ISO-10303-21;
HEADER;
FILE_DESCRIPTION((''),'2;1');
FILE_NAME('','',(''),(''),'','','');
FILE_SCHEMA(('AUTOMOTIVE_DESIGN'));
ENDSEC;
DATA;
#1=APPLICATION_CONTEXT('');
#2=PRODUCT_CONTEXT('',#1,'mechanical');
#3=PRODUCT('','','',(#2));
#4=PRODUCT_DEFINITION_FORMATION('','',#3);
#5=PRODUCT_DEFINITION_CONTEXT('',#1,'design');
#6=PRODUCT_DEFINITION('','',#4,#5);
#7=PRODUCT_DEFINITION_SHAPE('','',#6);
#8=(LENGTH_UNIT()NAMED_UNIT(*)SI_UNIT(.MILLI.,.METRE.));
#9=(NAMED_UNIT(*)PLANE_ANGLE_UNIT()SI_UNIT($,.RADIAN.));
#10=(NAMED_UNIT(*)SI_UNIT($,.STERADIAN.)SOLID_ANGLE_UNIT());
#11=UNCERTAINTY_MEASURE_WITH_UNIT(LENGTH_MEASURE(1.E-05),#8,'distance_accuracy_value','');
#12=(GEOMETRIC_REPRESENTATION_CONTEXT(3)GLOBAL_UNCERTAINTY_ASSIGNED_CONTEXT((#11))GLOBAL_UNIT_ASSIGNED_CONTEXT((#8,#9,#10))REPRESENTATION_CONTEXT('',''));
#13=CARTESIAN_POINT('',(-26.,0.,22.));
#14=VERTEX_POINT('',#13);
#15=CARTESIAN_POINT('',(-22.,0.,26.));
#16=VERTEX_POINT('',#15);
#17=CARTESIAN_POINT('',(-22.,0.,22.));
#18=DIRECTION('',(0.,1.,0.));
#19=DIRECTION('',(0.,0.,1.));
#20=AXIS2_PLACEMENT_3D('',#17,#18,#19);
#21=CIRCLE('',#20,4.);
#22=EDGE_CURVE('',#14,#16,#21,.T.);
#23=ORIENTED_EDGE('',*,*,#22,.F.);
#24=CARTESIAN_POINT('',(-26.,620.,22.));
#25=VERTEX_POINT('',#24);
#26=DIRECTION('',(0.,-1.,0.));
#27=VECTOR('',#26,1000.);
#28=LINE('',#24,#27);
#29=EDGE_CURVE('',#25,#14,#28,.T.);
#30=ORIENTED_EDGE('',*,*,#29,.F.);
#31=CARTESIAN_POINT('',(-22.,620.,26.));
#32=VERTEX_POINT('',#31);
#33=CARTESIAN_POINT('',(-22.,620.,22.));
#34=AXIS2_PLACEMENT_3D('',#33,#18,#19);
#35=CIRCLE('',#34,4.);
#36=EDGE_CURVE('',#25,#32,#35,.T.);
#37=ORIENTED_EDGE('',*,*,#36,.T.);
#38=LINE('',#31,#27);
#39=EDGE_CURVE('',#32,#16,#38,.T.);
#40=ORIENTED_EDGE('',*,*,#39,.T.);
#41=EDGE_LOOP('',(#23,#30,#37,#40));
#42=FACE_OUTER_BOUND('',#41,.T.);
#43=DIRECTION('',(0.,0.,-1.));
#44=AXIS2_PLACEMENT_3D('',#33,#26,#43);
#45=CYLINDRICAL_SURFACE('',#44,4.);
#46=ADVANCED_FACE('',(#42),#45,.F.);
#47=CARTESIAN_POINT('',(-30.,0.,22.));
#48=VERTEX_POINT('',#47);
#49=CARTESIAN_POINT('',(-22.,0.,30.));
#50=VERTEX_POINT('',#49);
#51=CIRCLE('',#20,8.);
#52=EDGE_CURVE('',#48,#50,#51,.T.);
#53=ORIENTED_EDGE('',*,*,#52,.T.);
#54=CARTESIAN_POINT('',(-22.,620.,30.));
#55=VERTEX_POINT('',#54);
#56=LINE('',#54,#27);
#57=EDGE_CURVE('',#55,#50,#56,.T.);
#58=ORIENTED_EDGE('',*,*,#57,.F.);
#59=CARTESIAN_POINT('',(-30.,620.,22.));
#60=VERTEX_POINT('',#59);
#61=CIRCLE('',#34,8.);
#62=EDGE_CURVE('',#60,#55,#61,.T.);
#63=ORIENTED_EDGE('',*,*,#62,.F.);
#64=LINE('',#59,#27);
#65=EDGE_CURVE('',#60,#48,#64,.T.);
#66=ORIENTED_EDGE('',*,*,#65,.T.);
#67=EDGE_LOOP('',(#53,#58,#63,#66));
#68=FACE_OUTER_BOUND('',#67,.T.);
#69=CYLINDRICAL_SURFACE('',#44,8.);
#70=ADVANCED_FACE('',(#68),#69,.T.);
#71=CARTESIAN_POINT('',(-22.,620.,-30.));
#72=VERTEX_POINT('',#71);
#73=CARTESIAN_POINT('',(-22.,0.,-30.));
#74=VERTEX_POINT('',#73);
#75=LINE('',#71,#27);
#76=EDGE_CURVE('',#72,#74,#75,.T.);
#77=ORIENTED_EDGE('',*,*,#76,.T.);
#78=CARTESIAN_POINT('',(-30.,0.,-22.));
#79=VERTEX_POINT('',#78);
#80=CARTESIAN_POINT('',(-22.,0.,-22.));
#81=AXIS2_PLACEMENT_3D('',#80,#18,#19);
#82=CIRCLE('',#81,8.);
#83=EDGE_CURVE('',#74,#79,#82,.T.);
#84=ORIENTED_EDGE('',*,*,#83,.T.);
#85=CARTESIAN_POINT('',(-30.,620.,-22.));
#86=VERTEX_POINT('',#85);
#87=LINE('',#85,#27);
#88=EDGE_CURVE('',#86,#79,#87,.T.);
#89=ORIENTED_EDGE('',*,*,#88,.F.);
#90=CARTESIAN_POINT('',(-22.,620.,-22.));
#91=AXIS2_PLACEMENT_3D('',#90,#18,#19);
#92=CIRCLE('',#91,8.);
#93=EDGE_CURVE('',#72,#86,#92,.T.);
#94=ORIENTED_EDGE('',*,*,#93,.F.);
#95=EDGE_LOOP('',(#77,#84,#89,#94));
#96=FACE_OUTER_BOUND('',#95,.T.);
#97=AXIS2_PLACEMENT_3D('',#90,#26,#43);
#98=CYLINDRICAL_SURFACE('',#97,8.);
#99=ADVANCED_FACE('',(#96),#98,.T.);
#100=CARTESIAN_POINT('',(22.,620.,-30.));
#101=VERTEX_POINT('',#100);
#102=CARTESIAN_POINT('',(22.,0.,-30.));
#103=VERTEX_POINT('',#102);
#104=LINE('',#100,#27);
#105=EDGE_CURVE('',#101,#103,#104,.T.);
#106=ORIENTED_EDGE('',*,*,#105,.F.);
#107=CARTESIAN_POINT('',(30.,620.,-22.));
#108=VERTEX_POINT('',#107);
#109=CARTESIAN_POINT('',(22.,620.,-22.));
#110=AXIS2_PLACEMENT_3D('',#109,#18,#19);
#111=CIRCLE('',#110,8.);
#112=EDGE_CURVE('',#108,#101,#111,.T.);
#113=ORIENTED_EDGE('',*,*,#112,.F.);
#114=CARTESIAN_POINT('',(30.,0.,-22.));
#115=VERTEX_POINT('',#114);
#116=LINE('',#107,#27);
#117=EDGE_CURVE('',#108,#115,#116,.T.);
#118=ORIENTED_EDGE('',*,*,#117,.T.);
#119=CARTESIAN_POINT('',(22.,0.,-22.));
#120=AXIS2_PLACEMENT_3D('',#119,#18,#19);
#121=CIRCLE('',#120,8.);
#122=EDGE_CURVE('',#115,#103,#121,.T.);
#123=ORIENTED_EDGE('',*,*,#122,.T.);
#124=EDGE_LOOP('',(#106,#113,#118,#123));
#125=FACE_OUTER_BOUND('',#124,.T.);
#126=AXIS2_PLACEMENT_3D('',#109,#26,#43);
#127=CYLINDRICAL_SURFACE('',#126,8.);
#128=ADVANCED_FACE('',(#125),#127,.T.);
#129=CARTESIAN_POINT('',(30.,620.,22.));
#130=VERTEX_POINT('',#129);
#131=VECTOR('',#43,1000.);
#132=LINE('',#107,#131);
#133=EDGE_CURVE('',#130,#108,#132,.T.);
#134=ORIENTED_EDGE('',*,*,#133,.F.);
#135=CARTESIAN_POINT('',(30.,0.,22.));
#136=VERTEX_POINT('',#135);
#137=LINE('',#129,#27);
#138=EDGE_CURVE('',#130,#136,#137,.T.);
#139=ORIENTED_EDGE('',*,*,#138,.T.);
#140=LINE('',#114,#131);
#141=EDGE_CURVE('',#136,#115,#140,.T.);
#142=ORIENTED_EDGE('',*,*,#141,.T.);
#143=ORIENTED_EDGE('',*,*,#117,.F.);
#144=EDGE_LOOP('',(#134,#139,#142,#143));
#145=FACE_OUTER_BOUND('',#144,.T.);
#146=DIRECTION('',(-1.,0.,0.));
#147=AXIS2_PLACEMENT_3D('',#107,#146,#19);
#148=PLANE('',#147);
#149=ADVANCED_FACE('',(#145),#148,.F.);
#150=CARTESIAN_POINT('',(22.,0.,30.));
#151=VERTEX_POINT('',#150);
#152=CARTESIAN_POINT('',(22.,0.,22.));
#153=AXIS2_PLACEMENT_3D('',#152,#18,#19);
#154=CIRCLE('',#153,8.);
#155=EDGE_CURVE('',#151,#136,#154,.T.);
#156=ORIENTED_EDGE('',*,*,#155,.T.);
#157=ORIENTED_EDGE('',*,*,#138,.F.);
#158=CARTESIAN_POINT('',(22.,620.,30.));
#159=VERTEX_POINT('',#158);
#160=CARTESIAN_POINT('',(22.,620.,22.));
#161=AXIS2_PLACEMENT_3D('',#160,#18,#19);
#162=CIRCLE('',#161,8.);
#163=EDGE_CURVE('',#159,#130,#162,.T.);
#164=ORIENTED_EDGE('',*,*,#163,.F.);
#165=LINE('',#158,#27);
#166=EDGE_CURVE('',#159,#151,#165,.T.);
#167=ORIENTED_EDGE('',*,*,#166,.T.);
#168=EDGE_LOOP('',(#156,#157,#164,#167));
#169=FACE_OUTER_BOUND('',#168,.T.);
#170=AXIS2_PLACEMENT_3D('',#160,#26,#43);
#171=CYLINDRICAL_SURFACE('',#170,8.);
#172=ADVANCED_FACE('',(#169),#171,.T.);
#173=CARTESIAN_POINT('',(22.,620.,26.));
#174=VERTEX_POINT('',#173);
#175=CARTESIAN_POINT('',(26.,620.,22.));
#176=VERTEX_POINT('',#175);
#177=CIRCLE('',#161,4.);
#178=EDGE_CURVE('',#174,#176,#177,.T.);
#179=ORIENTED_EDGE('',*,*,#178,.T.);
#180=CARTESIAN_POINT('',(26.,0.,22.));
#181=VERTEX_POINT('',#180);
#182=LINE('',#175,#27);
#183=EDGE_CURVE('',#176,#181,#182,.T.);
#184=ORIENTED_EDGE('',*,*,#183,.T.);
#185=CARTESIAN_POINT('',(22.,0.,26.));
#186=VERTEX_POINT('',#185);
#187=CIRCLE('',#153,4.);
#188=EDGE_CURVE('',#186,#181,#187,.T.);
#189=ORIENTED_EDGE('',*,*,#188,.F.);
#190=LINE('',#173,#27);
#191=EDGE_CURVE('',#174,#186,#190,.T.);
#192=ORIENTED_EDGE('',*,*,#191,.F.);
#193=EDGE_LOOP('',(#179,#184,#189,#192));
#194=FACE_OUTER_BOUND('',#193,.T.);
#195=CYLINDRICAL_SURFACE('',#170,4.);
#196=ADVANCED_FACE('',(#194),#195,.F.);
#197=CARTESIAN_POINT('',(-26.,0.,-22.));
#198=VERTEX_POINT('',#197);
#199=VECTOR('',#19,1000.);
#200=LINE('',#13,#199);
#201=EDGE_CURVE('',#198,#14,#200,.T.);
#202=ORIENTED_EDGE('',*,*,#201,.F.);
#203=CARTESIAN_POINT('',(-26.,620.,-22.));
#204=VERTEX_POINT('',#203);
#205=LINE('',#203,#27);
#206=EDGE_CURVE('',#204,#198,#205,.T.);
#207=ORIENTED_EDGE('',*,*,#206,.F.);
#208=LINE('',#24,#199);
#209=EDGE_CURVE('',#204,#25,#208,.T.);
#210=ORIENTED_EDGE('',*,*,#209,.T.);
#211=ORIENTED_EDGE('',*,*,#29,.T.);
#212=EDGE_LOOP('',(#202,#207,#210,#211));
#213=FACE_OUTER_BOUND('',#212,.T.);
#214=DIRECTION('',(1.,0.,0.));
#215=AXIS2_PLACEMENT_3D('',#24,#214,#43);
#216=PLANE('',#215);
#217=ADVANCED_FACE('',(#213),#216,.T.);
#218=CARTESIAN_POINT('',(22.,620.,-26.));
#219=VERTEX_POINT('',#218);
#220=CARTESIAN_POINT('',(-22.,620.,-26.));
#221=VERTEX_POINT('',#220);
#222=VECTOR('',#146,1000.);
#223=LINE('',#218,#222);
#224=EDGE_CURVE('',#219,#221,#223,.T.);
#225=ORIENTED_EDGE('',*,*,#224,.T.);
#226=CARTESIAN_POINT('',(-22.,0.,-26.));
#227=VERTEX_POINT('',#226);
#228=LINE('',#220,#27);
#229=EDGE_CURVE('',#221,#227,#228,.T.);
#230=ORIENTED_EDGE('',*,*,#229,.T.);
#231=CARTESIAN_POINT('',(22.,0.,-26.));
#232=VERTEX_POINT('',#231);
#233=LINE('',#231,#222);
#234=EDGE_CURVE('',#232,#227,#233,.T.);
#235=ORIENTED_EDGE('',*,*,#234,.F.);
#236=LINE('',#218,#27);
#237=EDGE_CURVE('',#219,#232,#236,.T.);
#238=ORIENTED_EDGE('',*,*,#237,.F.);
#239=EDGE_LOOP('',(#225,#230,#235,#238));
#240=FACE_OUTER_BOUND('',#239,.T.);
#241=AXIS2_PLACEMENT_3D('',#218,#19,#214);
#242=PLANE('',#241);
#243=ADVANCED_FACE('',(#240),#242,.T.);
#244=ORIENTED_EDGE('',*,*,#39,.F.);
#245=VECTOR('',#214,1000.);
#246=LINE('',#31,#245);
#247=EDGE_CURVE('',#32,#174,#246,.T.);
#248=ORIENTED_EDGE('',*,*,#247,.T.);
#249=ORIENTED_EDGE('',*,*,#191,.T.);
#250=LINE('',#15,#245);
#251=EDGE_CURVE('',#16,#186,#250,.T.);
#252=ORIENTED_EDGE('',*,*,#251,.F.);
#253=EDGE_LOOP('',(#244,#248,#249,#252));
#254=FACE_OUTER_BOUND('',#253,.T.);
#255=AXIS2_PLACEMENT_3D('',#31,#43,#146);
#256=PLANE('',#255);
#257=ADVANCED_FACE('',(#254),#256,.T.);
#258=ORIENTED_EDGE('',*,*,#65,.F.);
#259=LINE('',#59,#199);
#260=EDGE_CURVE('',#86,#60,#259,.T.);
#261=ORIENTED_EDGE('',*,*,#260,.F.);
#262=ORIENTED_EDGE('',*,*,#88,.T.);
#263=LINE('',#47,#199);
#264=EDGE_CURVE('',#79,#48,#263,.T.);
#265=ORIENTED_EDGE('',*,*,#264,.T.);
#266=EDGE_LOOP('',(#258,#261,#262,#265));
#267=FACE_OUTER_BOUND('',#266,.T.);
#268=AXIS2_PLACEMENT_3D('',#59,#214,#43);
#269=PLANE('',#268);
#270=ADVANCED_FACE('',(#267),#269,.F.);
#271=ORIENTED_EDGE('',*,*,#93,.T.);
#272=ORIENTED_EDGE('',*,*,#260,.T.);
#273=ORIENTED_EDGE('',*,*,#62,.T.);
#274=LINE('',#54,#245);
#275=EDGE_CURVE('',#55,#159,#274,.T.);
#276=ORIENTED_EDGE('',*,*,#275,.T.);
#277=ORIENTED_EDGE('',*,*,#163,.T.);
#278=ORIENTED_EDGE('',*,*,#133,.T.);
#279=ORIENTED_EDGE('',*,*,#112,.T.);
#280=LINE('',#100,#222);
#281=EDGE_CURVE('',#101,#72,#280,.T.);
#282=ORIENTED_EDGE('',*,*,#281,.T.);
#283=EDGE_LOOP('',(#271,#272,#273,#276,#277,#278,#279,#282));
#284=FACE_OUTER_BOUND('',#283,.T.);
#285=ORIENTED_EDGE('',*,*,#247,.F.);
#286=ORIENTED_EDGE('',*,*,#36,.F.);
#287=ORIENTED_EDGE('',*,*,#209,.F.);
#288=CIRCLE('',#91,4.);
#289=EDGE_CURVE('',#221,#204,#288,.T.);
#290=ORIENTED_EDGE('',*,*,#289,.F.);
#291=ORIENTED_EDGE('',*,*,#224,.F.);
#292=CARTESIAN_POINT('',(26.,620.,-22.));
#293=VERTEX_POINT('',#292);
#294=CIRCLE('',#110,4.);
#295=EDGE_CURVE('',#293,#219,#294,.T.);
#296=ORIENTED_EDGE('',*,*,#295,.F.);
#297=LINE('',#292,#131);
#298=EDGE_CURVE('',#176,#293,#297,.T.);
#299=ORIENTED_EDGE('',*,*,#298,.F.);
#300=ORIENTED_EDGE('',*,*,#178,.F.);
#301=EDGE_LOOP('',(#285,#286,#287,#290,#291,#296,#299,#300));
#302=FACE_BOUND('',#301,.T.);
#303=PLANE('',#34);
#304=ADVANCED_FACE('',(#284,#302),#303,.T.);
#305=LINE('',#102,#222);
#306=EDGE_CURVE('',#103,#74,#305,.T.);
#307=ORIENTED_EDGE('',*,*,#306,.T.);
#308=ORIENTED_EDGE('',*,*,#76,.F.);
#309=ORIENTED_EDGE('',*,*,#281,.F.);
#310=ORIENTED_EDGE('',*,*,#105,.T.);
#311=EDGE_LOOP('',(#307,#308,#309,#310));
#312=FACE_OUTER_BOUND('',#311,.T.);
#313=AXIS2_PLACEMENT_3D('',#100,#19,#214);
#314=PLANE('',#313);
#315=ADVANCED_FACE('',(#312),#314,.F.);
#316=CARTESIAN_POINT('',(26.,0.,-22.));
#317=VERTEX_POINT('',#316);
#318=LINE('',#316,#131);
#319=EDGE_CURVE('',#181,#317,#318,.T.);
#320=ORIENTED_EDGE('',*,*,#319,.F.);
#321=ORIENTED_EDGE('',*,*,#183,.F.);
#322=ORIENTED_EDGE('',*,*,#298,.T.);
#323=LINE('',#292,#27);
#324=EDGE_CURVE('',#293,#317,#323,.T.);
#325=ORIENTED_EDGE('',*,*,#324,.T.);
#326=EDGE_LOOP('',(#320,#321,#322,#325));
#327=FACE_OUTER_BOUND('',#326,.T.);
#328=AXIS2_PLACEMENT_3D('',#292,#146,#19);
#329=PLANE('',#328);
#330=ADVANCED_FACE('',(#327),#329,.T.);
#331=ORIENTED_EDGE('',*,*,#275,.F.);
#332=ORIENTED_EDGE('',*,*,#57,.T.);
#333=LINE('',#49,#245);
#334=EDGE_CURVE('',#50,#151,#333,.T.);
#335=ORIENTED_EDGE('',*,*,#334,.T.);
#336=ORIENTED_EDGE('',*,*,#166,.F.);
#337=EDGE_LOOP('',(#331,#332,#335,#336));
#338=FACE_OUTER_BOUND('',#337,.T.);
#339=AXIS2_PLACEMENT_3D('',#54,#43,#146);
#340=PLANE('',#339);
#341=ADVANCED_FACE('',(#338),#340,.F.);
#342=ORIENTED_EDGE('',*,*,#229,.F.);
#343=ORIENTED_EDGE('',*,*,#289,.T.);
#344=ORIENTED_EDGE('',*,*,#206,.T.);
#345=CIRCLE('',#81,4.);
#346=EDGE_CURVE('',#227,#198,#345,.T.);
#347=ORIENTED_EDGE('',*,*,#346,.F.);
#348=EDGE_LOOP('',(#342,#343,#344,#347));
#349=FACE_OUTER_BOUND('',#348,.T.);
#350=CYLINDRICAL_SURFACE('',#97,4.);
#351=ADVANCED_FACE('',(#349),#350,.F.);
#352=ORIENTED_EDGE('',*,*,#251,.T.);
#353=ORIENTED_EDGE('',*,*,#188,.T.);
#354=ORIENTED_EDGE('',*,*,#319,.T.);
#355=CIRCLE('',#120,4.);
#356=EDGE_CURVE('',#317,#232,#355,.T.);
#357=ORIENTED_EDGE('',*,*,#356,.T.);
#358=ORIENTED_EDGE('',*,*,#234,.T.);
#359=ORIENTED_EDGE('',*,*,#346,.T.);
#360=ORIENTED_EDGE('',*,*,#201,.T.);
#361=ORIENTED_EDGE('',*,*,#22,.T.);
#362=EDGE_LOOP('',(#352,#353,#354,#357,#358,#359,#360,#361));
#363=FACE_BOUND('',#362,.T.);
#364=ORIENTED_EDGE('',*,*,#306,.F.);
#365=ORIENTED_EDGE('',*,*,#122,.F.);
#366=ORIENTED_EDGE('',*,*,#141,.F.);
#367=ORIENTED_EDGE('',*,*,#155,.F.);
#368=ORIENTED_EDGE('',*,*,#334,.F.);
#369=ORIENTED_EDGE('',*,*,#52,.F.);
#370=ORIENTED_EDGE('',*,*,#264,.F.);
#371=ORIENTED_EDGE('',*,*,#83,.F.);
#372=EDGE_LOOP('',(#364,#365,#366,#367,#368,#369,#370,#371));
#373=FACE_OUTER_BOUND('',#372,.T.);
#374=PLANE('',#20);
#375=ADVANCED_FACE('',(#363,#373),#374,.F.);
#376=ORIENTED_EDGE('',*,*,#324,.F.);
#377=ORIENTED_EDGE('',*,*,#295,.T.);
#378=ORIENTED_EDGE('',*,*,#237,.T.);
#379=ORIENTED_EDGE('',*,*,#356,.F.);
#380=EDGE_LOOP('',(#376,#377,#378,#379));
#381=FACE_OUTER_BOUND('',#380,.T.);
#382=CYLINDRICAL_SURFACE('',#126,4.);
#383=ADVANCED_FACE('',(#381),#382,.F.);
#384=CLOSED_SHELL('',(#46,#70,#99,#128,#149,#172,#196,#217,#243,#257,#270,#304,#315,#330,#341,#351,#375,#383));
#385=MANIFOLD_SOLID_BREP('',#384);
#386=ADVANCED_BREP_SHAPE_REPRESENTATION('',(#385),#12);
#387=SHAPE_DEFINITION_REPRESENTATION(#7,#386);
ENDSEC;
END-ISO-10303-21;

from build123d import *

# Parameters (mm, degrees)
GB_T_6728_2002_SQUARE_HOLLOW_SECTION_60_DEPTH = 620


with BuildPart() as part:
    # Sketch1 → GB/T 6728-2002 square hollow section 60×60×4(1) (new body)
    with BuildSketch(Plane(origin=(0, 0, 0), x_dir=(-1, 0, 0), z_dir=(0, 1, 0))):
        with BuildLine():
            Line((-22, -30), (22, -30))
            ThreePointArc((22, -30), (27.656854249, -27.656854249), (30, -22))
            Line((30, -22), (30, 22))
            ThreePointArc((30, 22), (27.656854249, 27.656854249), (22, 30))
            Line((22, 30), (-22, 30))
            ThreePointArc((-22, 30), (-27.656854249, 27.656854249), (-30, 22))
            Line((-30, 22), (-30, -22))
            ThreePointArc((-30, -22), (-27.656854249, -27.656854249), (-22, -30))
        make_face()
        with BuildLine():
            Line((-22, -26), (22, -26))
            ThreePointArc((22, -26), (24.828427125, -24.828427125), (26, -22))
            Line((26, -22), (26, 22))
            ThreePointArc((26, 22), (24.828427125, 24.828427125), (22, 26))
            Line((22, 26), (-22, 26))
            ThreePointArc((-22, 26), (-24.828427125, 24.828427125), (-26, 22))
            Line((-26, 22), (-26, -22))
            ThreePointArc((-26, -22), (-24.828427125, -24.828427125), (-22, -26))
        make_face(mode=Mode.SUBTRACT)
    extrude(amount=GB_T_6728_2002_SQUARE_HOLLOW_SECTION_60_DEPTH)


solid = part.part
